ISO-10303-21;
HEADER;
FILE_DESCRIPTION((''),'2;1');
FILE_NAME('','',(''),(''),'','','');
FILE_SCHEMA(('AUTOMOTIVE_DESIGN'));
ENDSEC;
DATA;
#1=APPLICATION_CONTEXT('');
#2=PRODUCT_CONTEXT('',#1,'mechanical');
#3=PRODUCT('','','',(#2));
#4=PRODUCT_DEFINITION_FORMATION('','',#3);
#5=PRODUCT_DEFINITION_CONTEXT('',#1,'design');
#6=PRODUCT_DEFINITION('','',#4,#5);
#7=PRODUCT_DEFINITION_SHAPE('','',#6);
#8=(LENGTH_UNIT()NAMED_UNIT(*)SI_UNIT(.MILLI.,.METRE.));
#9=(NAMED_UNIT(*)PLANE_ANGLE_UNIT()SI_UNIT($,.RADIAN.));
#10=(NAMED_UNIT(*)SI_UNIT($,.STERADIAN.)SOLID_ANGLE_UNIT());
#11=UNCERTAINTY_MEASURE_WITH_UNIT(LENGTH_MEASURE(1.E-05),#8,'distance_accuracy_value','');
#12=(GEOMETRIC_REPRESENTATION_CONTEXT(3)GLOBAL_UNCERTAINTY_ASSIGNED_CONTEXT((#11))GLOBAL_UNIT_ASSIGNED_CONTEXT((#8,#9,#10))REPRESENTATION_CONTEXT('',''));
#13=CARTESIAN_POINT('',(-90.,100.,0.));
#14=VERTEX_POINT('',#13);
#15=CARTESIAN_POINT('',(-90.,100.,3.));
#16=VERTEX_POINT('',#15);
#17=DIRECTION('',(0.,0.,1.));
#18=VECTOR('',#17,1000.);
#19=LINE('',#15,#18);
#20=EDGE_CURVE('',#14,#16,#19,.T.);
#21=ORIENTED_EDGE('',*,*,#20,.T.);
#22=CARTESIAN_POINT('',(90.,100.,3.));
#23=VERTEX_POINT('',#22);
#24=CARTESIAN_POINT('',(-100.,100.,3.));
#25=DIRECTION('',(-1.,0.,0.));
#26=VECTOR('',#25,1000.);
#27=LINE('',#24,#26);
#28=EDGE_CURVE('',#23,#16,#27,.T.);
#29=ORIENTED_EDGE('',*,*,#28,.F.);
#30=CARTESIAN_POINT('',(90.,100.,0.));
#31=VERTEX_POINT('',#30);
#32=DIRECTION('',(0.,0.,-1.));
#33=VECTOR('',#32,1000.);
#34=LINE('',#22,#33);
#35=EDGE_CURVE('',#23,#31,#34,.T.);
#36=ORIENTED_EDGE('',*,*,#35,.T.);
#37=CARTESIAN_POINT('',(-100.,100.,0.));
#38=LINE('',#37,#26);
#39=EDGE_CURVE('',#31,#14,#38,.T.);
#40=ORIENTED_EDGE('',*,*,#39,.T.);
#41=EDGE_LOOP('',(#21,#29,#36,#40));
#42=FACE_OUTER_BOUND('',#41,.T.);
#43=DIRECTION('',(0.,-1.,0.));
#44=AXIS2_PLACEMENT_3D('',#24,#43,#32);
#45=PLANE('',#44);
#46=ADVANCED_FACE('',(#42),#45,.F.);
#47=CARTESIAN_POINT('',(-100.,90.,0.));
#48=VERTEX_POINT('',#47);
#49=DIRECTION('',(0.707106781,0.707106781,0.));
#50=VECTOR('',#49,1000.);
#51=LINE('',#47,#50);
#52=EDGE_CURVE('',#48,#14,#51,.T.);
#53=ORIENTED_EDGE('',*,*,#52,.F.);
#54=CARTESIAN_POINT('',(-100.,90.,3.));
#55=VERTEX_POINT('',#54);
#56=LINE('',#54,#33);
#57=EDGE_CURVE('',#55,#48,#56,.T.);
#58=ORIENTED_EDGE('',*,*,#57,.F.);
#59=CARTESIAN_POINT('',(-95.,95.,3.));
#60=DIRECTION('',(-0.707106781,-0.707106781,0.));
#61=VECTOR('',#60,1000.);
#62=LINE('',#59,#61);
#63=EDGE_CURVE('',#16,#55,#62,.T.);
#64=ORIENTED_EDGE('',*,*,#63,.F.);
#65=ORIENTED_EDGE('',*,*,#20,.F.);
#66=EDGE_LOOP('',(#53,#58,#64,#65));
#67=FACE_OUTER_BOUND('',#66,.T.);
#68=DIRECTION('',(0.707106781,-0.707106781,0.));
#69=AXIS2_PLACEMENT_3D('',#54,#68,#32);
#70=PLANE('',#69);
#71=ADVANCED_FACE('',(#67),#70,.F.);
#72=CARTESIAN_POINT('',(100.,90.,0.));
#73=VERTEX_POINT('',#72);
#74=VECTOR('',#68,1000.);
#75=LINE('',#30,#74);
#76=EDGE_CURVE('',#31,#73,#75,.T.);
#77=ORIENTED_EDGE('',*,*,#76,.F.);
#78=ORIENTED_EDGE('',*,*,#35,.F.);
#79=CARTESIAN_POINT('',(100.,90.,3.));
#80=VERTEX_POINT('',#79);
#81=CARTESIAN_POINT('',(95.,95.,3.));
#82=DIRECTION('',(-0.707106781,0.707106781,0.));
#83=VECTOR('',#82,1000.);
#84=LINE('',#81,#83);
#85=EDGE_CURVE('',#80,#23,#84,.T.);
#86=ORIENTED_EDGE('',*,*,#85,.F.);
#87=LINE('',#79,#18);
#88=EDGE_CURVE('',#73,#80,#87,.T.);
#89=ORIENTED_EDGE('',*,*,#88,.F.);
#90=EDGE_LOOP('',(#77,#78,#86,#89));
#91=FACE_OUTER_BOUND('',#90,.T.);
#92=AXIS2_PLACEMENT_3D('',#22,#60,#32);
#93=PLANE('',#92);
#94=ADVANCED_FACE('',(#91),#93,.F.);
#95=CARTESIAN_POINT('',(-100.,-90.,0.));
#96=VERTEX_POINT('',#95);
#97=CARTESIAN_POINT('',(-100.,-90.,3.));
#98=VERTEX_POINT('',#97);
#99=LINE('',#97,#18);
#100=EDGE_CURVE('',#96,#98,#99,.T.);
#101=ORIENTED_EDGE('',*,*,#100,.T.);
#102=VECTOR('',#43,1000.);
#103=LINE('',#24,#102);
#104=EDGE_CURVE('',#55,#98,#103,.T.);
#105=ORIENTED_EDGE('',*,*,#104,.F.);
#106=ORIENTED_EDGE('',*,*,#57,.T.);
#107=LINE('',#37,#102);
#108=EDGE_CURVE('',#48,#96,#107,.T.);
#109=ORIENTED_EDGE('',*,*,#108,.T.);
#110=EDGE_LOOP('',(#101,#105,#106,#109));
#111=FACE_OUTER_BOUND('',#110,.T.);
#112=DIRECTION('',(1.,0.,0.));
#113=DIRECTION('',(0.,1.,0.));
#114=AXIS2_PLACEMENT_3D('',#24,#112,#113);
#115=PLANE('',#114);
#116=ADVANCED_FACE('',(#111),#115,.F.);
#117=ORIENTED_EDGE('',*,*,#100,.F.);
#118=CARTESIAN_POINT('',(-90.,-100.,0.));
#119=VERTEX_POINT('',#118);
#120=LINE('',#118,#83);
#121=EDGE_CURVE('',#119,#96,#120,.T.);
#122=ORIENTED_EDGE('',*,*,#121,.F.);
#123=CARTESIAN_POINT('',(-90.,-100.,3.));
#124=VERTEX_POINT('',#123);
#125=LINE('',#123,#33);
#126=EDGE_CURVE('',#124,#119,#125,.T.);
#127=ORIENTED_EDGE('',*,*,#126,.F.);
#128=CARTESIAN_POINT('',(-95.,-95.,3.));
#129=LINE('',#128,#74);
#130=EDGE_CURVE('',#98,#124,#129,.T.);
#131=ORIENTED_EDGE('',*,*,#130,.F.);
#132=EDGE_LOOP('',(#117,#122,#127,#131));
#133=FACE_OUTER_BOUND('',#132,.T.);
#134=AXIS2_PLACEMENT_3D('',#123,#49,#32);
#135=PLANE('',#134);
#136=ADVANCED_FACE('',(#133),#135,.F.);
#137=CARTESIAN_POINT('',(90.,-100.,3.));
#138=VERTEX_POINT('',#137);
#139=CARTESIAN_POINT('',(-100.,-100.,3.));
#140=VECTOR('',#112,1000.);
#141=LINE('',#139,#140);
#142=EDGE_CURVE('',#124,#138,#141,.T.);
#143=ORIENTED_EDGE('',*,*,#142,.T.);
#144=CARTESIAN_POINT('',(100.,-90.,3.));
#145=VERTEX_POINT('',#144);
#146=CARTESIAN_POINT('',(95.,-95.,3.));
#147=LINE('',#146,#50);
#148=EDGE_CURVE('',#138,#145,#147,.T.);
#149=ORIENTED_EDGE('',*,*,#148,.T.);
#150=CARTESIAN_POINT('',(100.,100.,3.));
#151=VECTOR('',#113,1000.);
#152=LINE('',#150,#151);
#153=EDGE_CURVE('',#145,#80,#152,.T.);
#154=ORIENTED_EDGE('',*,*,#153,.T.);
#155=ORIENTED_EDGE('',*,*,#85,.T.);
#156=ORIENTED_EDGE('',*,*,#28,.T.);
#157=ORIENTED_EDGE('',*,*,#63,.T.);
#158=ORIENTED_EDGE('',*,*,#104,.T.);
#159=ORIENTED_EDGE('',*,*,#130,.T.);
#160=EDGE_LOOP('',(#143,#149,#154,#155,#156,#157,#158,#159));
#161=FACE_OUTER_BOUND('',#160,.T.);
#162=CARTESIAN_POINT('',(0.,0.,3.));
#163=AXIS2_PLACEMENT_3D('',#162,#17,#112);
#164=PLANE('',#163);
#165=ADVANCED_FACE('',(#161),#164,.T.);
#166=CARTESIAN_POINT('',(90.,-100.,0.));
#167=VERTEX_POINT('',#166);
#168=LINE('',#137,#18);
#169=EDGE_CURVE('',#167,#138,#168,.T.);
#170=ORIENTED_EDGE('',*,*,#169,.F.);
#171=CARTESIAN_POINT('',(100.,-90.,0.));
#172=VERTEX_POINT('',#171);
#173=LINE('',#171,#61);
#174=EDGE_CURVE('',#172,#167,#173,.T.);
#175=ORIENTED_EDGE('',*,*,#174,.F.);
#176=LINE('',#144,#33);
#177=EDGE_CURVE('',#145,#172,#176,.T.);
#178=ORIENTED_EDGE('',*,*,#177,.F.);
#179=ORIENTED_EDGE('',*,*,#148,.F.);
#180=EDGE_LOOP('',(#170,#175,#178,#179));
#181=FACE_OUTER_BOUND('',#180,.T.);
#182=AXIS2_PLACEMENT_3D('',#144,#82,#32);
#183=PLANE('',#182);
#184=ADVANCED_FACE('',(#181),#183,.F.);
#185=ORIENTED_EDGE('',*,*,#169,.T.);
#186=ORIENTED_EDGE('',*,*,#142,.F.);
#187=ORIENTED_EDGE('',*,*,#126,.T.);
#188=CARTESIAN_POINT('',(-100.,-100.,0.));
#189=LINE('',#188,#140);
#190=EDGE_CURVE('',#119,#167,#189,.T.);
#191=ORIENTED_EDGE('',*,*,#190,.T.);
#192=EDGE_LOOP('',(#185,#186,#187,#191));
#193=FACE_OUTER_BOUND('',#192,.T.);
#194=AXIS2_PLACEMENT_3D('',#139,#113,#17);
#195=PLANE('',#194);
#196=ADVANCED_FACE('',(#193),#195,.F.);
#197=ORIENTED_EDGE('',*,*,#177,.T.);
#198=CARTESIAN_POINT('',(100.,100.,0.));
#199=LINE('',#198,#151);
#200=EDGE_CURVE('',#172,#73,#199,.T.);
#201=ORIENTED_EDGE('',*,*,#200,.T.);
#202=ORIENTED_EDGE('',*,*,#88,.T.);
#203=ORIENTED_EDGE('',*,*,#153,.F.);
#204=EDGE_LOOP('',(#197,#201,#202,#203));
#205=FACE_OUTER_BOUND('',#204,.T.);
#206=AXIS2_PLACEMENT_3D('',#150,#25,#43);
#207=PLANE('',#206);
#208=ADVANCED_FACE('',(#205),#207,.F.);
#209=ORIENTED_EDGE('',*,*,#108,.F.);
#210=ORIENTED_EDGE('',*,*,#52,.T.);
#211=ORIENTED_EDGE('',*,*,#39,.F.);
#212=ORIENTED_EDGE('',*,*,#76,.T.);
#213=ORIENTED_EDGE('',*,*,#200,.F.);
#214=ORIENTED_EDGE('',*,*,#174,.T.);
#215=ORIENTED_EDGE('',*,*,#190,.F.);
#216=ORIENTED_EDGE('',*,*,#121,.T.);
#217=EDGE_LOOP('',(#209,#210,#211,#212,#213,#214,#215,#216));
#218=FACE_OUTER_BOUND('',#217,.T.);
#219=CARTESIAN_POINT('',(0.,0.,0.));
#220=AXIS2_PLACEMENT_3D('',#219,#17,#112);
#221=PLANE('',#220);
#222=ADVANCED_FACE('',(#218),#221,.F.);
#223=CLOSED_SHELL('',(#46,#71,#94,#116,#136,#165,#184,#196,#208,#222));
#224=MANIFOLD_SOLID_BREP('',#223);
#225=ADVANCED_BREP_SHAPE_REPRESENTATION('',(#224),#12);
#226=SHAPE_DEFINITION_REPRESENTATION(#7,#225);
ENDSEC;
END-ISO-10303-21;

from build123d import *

# Parameters (mm, degrees)
SKETCH_1_W      = 200
SKETCH_1_H      = 200
EXTRUDE_1_DEPTH = 3
CHAMFER_1_SIZE  = 10


with BuildPart() as part:
    # 草图1 → 凸台-拉伸1 (new body)
    with BuildSketch(Plane.XY):
        Rectangle(SKETCH_1_W, SKETCH_1_H)
    extrude(amount=EXTRUDE_1_DEPTH)

    # 倒角1
    chamfer_1_edges = [part.edges().sort_by_distance(p)[0] for p in [
        (100, -100, 1.5),
        (-100, -100, 1.5),
        (-100, 100, 1.5),
        (100, 100, 1.5),
    ]]
    chamfer(chamfer_1_edges, length=CHAMFER_1_SIZE)


solid = part.part
